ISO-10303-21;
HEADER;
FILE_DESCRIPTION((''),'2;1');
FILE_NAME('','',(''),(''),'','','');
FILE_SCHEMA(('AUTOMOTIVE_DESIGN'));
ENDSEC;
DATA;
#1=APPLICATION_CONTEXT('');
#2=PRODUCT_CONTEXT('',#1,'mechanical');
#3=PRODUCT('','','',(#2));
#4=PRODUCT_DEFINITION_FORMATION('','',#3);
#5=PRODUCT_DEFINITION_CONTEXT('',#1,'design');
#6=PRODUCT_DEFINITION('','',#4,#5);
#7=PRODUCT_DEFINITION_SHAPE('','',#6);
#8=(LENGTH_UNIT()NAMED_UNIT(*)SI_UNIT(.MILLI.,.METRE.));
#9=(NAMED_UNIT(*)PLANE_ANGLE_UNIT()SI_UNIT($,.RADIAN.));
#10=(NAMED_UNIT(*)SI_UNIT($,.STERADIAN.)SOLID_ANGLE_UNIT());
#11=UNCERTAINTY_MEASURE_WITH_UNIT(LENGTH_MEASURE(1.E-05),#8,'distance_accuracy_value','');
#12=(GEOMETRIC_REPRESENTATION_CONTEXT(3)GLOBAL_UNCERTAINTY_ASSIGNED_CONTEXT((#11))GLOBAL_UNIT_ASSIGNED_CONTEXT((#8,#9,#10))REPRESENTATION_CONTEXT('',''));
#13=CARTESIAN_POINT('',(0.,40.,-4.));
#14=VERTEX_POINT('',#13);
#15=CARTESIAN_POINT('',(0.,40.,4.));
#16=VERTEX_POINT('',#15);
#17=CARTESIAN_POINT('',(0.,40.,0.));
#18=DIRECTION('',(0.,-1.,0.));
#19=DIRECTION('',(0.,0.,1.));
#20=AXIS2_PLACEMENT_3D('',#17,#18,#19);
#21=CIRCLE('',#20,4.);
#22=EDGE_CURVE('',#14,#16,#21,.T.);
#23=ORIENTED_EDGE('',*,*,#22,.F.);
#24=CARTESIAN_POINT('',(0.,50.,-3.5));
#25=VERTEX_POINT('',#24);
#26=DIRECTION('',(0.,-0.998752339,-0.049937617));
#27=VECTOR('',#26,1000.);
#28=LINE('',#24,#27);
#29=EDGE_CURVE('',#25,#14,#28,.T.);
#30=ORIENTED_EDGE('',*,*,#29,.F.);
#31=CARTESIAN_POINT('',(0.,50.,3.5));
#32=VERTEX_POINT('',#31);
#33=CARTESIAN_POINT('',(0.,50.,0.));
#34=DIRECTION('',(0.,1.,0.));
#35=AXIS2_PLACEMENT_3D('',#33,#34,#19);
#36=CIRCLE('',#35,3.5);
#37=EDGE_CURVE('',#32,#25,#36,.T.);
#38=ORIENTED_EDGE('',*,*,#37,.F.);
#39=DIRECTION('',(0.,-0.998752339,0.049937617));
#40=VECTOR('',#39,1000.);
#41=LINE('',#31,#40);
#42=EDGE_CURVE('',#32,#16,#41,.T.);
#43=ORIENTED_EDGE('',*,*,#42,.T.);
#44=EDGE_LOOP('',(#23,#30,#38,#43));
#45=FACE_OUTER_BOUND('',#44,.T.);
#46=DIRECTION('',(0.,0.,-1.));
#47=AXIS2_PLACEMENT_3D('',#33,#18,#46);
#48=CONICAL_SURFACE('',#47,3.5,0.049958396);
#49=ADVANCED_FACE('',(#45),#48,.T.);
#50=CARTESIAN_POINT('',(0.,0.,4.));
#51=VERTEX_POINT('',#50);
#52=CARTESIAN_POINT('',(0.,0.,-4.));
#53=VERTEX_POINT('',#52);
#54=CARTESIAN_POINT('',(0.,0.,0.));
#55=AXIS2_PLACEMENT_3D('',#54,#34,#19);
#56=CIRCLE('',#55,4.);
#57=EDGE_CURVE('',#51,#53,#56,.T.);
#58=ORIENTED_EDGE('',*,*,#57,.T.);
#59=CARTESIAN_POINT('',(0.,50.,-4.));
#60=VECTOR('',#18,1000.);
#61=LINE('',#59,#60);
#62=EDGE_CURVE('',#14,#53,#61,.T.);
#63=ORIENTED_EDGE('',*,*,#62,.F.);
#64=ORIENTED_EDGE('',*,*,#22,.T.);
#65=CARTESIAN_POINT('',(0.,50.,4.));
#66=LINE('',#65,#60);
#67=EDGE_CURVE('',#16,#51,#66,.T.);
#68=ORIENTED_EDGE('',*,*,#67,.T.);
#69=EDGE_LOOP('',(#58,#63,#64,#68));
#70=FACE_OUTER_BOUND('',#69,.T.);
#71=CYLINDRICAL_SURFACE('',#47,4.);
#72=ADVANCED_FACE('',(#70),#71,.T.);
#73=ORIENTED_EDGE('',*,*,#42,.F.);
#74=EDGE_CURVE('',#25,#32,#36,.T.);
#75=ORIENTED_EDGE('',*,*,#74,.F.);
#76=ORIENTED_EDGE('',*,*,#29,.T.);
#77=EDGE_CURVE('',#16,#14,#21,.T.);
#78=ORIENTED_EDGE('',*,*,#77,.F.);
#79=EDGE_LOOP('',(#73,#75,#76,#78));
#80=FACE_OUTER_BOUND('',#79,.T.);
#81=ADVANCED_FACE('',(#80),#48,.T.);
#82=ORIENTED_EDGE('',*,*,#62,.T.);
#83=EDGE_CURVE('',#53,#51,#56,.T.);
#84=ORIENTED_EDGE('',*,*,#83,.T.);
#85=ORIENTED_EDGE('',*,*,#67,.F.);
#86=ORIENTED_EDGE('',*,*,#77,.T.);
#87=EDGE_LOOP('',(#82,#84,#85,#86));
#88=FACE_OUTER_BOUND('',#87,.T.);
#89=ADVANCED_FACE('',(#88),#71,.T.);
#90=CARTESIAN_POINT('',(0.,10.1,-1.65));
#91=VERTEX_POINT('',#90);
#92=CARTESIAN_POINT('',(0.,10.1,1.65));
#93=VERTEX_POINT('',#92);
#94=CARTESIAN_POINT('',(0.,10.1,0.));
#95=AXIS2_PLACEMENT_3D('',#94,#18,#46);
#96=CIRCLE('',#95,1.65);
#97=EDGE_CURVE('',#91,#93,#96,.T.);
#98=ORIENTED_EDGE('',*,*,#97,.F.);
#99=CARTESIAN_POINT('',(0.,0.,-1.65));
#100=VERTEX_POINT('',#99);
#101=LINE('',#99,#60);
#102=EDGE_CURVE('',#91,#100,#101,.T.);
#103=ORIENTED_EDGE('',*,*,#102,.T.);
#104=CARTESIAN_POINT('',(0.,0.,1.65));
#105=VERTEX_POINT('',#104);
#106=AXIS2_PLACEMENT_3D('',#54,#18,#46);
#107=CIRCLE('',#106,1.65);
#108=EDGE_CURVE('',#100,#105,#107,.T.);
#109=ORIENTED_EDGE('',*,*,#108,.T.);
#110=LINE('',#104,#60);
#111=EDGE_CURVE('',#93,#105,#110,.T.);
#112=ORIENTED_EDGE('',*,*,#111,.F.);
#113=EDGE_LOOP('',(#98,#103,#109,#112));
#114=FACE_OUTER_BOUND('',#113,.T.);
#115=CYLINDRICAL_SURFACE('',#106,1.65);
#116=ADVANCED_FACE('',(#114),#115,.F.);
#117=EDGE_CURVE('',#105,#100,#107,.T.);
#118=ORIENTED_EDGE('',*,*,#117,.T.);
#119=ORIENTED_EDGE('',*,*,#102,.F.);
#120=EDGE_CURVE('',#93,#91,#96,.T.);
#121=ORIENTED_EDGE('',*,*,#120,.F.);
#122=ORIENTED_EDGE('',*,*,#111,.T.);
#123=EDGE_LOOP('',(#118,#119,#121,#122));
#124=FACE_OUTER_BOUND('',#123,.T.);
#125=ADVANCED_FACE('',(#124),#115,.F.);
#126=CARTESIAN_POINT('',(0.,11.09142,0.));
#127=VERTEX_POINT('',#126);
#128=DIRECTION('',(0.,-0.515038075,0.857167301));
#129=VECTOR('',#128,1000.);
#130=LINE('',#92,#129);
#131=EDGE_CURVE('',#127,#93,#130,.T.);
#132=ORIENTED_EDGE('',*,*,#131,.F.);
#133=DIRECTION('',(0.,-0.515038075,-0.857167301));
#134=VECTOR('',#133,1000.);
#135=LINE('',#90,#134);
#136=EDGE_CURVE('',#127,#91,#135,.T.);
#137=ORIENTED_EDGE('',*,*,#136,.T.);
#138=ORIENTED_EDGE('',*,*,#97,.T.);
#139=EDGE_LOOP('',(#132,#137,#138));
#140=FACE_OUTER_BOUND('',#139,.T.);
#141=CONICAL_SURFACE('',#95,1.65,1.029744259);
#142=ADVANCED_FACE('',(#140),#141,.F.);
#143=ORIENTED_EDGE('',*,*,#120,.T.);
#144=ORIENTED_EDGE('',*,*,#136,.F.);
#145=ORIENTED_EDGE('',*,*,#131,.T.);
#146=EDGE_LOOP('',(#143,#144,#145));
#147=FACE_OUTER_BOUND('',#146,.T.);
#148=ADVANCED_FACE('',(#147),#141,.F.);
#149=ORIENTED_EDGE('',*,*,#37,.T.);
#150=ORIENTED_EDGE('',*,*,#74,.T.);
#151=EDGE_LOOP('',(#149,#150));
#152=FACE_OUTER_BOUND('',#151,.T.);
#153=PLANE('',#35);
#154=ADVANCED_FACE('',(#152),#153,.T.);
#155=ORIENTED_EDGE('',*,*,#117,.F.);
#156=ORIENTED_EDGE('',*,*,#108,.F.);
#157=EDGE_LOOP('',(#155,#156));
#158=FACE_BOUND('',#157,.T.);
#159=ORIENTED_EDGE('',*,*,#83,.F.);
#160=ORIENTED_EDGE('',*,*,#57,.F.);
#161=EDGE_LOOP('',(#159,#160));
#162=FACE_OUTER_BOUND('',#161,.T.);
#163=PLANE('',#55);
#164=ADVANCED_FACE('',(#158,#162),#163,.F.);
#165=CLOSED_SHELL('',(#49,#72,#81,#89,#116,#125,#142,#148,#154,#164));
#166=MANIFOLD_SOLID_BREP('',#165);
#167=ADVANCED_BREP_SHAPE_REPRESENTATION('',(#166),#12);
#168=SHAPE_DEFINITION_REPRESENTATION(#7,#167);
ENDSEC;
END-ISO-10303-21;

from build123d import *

# Parameters (mm, degrees)
SKETCH1_R             = 4
BOSS_EXTRUDE1_DEPTH   = 50
CHAMFER1_SIZE         = 10
CHAMFER1_SIZE2        = 0.5
M4_TAPPED_HOLE1_D     = 3.3
M4_TAPPED_HOLE1_DEPTH = 10.1
M4_TAPPED_HOLE1_TIP   = 0.991420021


with BuildPart() as part:
    # Sketch1 → Boss-Extrude1 (new body)
    with BuildSketch(Plane(origin=(0, 0, 0), x_dir=(1, 0, 0), z_dir=(0, 1, 0))):
        with Locations(Location((0, 0, 0), (0, 0, 270))):
            Circle(SKETCH1_R)
    extrude(amount=BOSS_EXTRUDE1_DEPTH)

    # Chamfer1
    chamfer1_edges = [part.edges().sort_by_distance(p)[0] for p in [
        (0, 50, -4),
    ]]
    chamfer1_side = [part.faces().sort_by_distance(p)[0] for p in [
        (0, 25, -4),
    ]]
    chamfer(chamfer1_edges, length=CHAMFER1_SIZE, length2=CHAMFER1_SIZE2, reference=chamfer1_side[0])

    # M4 Tapped Hole1
    with Locations(Plane(origin=(0, 0, 0), x_dir=(-1, 0, 0), z_dir=(0, -1, 0))):
        with Locations((0, 0)):
            Hole(M4_TAPPED_HOLE1_D / 2, depth=M4_TAPPED_HOLE1_DEPTH)
            with Locations((0, 0, -(M4_TAPPED_HOLE1_DEPTH + M4_TAPPED_HOLE1_TIP / 2))):  # 118° drill point
                Cone(0, M4_TAPPED_HOLE1_D / 2, M4_TAPPED_HOLE1_TIP, mode=Mode.SUBTRACT)


solid = part.part
